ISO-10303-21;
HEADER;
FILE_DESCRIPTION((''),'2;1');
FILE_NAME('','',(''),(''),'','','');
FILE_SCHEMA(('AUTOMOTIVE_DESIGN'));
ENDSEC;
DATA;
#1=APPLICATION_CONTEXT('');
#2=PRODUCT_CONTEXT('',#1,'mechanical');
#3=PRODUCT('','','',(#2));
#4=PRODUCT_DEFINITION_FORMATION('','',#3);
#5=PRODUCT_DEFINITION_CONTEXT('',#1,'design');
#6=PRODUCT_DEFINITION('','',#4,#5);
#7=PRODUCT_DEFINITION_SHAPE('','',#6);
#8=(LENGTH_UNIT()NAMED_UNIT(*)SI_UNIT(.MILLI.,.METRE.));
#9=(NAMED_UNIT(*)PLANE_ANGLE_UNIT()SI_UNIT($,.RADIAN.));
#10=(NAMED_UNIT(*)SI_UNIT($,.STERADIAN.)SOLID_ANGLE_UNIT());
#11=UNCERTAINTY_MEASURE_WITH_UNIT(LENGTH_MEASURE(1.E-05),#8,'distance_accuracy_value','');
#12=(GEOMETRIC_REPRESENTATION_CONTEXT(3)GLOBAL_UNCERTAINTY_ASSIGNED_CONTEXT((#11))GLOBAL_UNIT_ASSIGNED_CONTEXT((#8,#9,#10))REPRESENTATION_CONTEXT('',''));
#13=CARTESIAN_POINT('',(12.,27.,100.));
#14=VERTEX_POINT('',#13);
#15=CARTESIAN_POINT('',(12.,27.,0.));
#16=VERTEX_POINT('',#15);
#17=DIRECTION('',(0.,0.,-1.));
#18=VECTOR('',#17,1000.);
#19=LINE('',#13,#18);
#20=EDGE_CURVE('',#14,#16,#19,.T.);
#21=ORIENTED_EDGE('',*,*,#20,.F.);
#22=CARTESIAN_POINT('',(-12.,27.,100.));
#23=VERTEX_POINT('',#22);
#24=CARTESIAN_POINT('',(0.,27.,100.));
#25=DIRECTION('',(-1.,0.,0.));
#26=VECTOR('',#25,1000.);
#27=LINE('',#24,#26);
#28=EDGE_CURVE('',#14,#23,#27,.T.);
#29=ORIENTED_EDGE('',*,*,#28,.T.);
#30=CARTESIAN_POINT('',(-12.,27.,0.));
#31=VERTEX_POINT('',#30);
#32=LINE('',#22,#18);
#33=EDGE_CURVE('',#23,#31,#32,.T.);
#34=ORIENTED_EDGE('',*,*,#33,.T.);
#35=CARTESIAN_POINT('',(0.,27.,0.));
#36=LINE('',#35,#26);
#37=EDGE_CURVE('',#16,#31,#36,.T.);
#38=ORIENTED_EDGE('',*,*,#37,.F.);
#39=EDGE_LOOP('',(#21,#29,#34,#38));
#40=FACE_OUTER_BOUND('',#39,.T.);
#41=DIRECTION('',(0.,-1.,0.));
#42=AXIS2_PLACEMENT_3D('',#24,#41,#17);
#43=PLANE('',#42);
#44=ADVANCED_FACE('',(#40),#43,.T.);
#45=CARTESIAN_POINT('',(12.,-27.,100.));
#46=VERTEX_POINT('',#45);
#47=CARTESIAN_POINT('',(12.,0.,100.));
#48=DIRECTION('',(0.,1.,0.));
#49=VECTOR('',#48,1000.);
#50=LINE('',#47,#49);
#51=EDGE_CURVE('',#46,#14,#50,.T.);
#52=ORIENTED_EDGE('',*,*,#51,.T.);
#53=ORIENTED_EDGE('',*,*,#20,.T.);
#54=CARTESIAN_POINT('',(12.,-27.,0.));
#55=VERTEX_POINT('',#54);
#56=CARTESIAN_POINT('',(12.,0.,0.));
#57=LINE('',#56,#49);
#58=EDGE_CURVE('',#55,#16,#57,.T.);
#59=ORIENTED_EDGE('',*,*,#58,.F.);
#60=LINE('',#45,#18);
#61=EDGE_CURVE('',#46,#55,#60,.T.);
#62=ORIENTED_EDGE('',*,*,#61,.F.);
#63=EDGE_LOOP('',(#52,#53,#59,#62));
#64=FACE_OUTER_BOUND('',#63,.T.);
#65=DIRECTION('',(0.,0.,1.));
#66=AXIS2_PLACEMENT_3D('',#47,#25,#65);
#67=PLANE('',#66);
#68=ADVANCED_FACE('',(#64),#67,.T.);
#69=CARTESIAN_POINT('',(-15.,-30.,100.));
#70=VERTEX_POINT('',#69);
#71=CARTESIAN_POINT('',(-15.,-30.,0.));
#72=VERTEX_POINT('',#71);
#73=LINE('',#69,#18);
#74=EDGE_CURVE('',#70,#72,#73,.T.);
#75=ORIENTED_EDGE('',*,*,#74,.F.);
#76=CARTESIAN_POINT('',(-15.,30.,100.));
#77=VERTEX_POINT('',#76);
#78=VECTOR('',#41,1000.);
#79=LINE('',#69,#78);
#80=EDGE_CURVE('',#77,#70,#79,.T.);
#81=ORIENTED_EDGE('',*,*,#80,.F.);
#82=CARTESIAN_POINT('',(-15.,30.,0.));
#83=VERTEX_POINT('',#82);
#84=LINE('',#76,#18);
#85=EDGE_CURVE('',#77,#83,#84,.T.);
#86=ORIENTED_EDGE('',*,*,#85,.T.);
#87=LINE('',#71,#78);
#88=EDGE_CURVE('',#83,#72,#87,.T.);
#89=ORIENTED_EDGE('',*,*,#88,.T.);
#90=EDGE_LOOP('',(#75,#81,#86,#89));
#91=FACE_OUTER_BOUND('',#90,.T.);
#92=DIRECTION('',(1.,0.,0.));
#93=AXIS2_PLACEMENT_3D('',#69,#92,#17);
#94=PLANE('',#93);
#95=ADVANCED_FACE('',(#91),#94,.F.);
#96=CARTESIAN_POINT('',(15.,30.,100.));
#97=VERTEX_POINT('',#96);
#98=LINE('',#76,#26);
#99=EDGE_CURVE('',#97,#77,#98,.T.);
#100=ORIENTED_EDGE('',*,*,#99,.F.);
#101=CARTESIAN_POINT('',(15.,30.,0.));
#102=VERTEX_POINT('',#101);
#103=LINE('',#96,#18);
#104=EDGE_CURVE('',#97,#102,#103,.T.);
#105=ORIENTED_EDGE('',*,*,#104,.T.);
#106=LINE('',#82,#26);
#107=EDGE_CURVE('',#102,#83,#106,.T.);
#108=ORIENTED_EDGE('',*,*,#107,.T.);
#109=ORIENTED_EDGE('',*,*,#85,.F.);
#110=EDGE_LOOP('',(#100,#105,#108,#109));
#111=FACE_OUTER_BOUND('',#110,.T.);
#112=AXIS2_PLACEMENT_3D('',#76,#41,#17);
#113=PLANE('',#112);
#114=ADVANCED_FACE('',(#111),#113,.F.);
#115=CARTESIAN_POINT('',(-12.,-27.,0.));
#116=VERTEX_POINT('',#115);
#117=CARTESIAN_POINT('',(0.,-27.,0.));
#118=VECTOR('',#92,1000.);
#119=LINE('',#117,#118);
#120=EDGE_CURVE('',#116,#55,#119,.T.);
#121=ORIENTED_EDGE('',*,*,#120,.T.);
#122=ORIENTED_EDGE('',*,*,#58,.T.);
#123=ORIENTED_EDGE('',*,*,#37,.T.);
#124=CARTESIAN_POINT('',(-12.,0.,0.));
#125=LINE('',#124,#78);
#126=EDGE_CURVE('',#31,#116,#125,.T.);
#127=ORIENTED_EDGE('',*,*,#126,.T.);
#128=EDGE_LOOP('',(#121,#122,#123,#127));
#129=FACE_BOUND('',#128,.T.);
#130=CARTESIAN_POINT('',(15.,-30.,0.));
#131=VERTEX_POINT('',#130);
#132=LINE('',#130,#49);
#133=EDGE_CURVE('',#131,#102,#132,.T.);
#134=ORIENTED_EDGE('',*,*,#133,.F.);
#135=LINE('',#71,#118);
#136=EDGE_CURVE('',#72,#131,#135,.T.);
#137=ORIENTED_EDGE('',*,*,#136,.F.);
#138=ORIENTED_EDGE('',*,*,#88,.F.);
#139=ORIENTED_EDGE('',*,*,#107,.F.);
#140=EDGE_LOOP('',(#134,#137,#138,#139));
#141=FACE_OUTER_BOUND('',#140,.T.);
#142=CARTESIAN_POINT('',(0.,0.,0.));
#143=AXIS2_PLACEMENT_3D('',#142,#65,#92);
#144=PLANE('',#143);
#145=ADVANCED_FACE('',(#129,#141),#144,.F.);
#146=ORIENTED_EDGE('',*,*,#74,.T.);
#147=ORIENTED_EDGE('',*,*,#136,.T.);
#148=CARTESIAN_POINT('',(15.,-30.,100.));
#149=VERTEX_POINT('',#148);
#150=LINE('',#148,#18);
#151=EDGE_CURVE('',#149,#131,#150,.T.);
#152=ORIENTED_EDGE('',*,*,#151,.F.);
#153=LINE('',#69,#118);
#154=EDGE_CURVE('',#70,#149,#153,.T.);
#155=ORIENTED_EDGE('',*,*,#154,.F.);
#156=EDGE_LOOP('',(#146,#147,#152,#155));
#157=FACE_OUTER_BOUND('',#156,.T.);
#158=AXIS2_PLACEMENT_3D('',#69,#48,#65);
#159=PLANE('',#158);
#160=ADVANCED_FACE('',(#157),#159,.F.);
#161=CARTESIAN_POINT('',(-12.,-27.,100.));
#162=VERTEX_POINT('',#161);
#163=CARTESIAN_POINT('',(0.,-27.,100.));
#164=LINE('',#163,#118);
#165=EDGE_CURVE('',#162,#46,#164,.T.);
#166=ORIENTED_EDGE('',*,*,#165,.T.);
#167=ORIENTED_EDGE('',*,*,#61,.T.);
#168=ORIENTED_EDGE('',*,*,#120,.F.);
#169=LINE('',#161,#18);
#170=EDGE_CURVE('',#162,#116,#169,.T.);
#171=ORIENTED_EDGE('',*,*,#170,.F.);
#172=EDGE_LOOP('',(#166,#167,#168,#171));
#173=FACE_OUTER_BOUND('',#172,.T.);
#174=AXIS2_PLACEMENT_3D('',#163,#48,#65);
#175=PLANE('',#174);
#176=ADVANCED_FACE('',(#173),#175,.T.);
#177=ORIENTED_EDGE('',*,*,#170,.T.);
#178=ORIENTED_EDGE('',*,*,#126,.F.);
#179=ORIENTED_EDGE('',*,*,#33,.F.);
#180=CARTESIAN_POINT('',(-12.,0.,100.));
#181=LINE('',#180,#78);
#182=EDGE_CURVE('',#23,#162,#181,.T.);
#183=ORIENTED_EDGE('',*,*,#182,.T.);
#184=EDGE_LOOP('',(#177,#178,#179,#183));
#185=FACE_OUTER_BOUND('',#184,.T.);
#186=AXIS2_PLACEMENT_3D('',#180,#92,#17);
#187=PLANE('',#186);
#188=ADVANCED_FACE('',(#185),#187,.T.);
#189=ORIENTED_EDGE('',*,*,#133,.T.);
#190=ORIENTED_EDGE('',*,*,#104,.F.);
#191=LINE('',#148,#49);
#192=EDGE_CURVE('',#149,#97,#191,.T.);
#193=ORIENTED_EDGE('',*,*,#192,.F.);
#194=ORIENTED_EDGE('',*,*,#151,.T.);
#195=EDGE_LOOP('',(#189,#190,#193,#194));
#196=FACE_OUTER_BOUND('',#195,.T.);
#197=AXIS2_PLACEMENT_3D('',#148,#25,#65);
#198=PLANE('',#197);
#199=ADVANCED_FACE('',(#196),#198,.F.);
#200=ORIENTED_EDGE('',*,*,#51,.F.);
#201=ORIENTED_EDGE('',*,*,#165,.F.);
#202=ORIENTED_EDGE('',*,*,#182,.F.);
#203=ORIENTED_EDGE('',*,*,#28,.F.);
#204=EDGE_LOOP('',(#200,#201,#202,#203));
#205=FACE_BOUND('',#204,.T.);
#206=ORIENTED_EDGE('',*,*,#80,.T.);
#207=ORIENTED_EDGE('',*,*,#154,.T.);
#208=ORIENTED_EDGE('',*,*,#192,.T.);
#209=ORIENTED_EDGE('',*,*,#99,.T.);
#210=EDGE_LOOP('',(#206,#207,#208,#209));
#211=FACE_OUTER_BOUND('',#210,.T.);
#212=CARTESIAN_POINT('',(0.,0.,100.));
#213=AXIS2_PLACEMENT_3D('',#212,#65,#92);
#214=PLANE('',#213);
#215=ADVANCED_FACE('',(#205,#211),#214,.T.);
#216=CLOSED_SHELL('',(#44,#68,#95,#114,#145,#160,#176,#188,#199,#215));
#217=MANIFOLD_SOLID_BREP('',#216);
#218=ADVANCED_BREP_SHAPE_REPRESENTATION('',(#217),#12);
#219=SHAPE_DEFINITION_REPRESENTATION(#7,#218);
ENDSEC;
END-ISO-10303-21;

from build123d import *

# Parameters (mm, degrees)
SKETCH_1_W      = 30
SKETCH_1_H      = 60
SKETCH_1_W_2    = 24
SKETCH_1_H_2    = 54
EXTRUDE_1_DEPTH = 100


with BuildPart() as part:
    # 草图1 → 拉伸-薄壁1 (new body)
    with BuildSketch(Plane.XY):
        Rectangle(SKETCH_1_W, SKETCH_1_H)
        Rectangle(SKETCH_1_W_2, SKETCH_1_H_2, mode=Mode.SUBTRACT)
    extrude(amount=EXTRUDE_1_DEPTH)


solid = part.part
